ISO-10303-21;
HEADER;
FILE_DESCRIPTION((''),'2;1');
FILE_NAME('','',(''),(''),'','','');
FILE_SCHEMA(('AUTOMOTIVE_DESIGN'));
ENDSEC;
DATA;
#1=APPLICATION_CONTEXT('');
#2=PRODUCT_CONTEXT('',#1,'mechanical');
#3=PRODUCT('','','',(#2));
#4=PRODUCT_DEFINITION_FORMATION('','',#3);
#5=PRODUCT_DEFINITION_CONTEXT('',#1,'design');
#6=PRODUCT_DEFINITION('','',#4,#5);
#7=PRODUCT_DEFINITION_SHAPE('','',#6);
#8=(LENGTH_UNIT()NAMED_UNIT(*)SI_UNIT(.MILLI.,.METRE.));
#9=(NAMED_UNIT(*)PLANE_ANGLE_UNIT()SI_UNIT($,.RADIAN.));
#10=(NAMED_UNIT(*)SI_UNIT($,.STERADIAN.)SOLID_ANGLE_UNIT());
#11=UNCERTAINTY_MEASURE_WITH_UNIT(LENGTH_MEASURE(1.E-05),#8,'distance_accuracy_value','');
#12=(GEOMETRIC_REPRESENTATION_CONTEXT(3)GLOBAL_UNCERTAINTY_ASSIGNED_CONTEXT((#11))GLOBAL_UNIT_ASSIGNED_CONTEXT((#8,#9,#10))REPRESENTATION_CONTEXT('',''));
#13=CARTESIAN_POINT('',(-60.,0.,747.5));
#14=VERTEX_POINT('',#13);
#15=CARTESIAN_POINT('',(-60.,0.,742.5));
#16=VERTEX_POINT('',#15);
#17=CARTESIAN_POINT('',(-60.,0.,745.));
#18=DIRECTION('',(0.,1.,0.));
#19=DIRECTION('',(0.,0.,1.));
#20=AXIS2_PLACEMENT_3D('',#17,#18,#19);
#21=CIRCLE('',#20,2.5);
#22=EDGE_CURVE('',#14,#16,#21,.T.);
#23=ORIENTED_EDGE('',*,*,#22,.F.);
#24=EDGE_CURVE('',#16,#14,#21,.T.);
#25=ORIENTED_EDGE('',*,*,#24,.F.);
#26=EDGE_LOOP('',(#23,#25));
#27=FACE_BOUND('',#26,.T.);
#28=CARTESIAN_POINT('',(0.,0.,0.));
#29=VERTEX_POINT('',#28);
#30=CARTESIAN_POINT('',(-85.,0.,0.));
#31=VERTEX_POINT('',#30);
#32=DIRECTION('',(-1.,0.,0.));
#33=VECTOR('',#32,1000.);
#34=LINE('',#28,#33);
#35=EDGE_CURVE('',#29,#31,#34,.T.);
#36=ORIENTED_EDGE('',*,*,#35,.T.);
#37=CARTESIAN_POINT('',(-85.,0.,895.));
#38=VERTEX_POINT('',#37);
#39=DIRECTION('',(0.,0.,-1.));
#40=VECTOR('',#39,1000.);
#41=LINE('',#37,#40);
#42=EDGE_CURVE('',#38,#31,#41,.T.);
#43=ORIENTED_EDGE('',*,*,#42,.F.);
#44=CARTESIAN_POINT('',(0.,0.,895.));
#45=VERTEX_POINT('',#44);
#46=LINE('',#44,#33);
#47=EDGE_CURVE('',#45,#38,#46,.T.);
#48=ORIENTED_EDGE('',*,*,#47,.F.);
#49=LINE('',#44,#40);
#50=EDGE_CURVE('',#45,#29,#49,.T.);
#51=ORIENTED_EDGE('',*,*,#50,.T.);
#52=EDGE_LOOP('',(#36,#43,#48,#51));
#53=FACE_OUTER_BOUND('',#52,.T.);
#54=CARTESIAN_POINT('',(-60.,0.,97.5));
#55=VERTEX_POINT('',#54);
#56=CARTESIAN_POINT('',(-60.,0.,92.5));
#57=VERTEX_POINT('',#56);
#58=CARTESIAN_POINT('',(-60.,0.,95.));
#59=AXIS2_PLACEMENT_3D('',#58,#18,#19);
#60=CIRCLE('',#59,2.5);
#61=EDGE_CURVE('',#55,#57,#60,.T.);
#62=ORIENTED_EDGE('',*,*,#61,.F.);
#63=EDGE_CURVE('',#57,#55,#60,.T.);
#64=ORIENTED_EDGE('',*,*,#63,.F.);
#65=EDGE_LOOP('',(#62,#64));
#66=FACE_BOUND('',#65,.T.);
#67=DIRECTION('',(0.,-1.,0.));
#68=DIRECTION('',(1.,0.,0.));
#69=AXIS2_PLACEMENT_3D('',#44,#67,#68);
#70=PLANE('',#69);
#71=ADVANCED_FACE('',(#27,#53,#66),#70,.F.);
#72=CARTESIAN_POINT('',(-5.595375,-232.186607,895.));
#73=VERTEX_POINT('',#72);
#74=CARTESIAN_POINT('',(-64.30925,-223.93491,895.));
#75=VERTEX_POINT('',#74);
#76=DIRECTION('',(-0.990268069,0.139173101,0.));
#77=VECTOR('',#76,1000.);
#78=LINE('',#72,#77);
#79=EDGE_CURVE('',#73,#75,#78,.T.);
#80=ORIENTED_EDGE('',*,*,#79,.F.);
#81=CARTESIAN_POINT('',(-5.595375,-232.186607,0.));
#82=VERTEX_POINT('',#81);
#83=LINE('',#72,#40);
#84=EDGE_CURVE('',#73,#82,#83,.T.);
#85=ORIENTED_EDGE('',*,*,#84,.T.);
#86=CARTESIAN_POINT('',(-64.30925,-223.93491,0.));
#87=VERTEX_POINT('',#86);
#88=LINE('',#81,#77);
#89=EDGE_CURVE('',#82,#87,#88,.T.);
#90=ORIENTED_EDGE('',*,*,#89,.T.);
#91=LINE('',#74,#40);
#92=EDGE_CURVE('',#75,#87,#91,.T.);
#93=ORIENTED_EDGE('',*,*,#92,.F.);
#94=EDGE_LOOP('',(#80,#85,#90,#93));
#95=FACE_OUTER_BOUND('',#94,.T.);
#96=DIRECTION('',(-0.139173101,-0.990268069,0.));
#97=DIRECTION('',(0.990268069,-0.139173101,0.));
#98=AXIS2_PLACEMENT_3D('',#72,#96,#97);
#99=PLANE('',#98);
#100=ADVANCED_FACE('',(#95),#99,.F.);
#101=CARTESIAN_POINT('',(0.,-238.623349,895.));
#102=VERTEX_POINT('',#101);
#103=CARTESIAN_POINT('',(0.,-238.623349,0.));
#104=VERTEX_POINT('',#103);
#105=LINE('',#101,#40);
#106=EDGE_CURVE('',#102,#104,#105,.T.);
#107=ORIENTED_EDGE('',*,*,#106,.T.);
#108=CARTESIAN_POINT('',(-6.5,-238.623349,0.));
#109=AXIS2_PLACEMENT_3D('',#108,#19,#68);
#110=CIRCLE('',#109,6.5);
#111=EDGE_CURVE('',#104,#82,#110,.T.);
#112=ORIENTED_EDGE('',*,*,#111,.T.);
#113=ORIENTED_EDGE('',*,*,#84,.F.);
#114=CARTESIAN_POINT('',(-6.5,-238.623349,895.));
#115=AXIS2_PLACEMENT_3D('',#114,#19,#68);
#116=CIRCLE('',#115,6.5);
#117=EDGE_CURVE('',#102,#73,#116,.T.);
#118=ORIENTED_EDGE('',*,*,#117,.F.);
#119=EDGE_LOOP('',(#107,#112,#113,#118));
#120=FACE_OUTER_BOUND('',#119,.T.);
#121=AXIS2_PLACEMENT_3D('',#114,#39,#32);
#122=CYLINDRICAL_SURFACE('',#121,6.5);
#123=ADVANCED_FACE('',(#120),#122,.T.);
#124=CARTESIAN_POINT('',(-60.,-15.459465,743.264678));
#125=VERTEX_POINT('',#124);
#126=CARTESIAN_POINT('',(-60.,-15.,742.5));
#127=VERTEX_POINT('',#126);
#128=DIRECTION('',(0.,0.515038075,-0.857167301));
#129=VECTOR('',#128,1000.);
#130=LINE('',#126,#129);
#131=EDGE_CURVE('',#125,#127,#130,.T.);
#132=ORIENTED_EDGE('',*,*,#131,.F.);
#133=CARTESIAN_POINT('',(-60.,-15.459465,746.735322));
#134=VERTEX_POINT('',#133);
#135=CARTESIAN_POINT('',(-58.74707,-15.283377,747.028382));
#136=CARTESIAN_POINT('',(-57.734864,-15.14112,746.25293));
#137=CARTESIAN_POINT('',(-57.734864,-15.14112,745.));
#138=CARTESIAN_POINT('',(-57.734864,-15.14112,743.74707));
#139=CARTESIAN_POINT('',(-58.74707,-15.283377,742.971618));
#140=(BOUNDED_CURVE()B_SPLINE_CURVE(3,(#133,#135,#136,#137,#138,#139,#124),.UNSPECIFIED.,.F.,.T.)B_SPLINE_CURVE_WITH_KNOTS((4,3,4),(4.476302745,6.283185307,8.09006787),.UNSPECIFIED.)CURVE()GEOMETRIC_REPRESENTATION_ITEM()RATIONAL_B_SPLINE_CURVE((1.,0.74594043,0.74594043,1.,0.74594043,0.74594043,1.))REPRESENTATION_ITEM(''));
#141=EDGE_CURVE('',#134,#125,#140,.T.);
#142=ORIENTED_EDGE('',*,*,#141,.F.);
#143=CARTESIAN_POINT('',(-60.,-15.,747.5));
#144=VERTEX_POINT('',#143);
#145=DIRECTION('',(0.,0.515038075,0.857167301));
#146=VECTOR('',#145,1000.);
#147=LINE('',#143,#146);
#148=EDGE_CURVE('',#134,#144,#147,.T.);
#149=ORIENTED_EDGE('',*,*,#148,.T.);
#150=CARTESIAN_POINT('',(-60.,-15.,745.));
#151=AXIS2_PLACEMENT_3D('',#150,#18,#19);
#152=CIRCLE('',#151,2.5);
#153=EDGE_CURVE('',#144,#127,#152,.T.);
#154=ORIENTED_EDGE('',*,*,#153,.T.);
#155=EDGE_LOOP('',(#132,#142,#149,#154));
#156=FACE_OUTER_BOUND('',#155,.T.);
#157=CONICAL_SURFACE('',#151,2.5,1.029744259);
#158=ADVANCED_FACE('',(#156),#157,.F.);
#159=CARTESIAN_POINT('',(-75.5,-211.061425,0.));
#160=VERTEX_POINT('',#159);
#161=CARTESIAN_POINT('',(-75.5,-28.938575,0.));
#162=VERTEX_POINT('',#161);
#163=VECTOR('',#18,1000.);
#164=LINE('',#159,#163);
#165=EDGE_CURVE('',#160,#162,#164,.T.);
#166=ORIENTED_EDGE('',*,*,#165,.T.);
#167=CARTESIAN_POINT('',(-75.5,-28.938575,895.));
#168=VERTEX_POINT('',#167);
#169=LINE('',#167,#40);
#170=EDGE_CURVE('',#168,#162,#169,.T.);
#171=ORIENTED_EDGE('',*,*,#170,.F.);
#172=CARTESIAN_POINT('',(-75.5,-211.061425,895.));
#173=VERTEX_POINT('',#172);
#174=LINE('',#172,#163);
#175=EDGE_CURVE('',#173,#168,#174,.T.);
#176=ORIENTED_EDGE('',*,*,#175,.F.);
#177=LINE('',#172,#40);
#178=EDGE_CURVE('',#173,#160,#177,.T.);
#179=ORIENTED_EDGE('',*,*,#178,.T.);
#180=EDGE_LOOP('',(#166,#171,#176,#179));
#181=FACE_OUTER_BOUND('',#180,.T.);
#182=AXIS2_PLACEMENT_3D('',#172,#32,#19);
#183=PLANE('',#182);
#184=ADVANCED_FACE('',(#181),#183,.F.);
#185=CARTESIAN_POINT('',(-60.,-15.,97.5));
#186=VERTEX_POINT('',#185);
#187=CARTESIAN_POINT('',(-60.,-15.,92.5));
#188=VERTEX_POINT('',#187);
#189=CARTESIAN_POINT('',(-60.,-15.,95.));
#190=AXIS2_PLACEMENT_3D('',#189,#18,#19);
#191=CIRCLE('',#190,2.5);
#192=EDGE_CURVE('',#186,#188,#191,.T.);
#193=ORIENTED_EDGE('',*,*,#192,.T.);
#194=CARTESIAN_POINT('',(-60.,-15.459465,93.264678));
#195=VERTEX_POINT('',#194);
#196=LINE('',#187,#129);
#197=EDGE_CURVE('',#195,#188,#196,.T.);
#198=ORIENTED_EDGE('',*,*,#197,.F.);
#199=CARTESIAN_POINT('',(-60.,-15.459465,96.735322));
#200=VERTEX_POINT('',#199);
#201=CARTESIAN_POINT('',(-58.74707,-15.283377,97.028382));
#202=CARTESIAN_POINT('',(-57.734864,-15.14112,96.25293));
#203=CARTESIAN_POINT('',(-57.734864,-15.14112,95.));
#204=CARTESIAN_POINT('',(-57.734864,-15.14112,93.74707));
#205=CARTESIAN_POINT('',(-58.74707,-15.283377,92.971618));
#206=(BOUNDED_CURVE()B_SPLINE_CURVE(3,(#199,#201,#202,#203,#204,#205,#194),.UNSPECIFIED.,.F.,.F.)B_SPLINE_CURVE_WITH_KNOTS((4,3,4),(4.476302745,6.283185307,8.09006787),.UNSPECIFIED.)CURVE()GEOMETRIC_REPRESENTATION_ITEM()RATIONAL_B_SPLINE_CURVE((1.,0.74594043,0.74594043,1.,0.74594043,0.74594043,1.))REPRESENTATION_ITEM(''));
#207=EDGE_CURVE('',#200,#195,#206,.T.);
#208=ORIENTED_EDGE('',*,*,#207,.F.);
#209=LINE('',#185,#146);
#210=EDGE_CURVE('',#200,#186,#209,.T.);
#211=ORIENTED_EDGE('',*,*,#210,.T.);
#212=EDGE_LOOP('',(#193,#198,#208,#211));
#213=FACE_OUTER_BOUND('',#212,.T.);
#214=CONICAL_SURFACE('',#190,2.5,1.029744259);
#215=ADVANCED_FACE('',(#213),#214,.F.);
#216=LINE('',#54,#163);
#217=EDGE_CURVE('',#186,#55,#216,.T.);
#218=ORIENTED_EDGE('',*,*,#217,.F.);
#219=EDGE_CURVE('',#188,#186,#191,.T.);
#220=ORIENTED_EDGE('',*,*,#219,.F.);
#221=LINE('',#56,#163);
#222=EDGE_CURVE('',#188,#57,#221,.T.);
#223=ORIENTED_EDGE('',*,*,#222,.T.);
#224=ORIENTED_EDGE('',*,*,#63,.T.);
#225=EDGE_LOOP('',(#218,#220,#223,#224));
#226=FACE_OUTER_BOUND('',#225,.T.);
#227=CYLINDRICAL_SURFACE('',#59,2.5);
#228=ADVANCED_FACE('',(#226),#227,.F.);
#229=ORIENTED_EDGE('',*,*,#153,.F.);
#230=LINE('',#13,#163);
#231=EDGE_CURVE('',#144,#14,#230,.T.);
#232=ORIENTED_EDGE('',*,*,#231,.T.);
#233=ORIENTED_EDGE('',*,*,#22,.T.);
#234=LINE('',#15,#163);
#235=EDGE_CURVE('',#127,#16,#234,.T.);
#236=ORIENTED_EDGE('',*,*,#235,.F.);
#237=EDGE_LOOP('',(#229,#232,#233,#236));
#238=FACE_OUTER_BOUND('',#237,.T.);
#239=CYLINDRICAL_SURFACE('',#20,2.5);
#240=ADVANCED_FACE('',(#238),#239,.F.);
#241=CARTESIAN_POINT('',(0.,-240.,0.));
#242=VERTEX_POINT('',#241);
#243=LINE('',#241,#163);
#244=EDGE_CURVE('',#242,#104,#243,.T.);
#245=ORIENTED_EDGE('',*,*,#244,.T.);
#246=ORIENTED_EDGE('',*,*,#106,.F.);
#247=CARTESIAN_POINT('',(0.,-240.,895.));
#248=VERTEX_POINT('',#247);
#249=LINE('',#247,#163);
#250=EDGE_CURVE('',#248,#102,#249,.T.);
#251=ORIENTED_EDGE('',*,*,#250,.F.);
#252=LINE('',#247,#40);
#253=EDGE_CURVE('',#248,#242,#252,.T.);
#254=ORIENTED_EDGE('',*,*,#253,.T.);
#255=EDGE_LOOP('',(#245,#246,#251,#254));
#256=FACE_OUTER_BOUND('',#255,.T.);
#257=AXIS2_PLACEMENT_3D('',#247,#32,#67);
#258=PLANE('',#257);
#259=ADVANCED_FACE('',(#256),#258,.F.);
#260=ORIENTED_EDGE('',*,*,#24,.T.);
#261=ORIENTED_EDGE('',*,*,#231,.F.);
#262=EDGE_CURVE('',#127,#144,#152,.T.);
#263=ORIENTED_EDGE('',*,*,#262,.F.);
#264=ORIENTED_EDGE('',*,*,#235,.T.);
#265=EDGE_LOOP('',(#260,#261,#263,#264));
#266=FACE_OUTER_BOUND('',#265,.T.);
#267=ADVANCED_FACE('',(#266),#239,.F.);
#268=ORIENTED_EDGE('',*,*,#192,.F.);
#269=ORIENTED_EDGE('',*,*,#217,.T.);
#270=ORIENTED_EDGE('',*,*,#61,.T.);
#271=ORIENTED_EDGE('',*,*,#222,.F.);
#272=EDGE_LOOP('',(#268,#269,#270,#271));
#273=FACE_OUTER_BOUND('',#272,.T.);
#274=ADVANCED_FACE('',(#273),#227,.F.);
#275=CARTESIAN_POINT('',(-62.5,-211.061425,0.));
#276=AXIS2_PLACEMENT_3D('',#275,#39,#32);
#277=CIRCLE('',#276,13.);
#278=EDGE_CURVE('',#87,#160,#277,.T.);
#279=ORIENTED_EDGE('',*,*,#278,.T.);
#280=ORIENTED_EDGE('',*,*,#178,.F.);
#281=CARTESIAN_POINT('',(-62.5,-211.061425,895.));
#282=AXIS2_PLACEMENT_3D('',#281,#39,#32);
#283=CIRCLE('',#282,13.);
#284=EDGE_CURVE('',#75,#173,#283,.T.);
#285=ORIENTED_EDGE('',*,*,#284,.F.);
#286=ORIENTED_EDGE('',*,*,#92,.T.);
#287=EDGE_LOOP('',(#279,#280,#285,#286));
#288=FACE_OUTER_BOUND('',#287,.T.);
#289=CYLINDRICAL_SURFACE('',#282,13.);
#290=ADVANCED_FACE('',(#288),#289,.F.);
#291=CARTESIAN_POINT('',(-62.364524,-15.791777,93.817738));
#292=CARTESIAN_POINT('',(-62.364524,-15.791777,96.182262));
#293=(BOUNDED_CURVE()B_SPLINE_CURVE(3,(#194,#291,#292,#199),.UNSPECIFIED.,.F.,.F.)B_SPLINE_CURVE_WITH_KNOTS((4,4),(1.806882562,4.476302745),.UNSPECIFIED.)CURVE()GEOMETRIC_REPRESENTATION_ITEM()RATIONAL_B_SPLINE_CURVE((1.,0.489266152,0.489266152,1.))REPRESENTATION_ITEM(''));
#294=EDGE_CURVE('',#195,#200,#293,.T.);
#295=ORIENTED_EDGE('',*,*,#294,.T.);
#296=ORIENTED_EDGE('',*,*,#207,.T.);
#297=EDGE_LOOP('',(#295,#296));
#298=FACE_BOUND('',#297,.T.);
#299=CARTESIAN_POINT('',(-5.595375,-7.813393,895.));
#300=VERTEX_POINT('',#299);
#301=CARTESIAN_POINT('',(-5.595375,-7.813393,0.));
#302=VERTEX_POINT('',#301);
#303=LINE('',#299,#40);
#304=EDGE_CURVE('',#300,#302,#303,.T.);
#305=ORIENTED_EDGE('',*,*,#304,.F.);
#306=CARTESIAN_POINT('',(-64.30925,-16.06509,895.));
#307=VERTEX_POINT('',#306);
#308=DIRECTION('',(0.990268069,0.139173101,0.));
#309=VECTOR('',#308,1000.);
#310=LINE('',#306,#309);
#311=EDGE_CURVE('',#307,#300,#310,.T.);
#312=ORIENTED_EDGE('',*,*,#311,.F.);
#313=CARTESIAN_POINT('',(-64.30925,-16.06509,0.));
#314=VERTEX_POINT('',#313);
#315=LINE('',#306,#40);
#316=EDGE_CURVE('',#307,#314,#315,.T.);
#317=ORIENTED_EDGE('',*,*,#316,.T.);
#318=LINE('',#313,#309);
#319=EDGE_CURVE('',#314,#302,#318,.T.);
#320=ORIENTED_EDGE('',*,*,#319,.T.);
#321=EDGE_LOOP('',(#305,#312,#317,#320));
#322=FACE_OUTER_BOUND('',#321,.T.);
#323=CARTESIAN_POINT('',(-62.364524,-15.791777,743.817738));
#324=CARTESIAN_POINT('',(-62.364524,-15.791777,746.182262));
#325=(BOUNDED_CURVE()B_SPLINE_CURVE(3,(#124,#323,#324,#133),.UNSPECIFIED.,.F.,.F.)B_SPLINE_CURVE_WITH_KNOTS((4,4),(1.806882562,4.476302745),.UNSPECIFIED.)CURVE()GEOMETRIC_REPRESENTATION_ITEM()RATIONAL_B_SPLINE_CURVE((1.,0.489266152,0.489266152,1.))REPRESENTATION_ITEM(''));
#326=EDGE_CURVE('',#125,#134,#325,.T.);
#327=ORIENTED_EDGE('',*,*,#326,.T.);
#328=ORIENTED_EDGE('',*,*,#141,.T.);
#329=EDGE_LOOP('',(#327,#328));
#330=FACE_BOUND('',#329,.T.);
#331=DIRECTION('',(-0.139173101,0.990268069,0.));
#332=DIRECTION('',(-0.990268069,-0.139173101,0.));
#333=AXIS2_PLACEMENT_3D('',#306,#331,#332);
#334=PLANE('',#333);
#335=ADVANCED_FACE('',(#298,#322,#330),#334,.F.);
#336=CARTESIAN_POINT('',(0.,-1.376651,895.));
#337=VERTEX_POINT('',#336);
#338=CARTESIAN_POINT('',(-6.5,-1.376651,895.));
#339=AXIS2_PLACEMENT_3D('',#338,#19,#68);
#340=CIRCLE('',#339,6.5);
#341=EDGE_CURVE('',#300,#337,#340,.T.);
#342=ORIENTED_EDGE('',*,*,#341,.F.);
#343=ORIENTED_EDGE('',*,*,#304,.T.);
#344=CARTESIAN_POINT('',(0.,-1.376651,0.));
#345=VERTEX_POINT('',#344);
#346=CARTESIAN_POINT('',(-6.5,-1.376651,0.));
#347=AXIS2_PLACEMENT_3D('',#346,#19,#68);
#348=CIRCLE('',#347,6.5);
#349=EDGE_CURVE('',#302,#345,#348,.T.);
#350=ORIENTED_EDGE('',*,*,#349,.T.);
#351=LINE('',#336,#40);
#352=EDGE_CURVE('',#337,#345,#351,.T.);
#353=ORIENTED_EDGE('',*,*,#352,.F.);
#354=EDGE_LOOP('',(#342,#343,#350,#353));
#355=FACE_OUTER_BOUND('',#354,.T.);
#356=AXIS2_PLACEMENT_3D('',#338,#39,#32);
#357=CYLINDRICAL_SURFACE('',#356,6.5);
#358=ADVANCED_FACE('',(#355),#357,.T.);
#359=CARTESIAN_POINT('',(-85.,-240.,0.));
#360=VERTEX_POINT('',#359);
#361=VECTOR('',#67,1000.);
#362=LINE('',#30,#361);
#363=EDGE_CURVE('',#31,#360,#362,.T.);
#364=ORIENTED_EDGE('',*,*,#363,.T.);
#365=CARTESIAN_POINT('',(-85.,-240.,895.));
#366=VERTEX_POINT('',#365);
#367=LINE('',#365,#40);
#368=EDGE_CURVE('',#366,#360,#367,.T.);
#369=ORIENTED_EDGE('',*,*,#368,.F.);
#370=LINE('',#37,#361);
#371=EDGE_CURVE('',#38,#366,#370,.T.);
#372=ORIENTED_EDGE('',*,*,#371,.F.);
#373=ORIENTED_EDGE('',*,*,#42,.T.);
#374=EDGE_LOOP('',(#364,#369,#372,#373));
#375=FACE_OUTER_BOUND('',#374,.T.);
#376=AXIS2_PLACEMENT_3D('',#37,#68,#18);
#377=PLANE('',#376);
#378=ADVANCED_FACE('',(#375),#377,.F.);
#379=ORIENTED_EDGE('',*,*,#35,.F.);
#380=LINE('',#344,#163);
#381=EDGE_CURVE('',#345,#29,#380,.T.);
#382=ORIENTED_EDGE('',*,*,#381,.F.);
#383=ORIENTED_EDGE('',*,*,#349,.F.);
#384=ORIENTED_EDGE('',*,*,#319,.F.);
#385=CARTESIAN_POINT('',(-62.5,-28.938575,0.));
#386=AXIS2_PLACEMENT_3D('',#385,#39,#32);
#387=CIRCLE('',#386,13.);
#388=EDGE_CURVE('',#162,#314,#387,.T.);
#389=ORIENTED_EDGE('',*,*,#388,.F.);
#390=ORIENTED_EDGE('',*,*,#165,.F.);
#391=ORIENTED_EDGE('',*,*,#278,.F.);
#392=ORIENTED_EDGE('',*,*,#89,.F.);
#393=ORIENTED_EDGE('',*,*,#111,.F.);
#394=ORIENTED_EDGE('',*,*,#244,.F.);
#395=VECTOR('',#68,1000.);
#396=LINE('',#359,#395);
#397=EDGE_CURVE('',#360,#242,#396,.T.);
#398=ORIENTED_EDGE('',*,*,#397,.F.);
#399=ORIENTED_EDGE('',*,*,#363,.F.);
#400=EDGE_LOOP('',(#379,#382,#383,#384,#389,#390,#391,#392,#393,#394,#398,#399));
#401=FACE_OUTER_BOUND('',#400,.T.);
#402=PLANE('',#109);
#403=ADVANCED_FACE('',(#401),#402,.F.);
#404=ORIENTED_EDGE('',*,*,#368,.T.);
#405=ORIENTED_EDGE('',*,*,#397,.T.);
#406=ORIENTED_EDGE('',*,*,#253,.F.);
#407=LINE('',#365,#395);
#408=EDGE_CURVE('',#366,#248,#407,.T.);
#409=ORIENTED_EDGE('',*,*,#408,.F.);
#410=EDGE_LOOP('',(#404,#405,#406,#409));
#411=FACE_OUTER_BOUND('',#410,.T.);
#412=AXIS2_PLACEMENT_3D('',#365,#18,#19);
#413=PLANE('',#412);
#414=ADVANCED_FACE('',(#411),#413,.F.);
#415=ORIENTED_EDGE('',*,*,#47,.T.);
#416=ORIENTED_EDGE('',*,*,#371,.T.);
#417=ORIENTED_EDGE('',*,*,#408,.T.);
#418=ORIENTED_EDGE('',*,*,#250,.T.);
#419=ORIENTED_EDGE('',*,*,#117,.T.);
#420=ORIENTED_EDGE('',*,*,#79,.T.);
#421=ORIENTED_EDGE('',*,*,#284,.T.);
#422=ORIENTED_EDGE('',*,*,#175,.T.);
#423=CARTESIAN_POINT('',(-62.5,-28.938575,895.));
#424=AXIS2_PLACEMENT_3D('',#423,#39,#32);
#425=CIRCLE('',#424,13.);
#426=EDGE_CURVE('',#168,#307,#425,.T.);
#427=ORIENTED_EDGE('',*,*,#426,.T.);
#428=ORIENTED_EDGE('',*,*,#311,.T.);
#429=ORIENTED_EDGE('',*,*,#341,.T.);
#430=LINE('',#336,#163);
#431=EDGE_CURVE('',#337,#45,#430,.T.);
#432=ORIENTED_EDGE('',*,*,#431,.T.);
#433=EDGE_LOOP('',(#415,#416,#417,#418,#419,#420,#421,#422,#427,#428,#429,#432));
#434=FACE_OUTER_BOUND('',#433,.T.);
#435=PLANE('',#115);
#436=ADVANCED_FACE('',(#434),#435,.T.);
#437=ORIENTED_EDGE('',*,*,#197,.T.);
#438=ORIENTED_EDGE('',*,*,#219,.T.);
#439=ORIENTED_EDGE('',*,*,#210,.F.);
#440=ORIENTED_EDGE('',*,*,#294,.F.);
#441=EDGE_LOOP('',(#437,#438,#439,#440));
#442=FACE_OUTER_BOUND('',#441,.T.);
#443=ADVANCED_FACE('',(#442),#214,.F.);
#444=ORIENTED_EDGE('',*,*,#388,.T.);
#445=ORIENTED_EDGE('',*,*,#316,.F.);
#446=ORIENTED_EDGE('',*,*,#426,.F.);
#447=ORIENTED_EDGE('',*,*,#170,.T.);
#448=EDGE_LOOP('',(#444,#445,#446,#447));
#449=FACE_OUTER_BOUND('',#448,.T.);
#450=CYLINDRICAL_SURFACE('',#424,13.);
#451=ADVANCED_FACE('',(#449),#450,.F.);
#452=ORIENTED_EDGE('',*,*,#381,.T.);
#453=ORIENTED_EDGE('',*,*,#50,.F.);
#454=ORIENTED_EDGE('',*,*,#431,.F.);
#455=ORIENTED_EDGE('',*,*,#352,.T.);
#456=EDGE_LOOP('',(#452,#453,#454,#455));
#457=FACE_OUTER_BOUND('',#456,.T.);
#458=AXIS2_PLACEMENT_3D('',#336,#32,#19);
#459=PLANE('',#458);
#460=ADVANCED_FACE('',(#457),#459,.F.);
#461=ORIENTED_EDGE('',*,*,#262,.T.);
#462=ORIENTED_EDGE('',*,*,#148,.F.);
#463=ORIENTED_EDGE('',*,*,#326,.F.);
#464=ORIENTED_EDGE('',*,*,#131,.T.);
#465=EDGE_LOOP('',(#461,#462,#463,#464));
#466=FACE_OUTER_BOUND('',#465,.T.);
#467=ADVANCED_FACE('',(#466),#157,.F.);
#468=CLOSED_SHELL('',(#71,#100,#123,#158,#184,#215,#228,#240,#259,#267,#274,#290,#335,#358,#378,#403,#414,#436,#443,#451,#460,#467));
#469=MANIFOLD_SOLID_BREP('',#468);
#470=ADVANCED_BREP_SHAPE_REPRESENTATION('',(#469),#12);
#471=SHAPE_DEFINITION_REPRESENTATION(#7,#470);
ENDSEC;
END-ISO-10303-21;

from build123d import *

# Parameters (mm, degrees)
EXTRUDE_1_DEPTH        = 895
HOLE_WIZARD_M6_1_D     = 5
HOLE_WIZARD_M6_1_DEPTH = 15
HOLE_WIZARD_M6_1_TIP   = 1.502151548


with BuildPart() as part:
    # 草图1 → 凸台-拉伸1 (new body)
    with BuildSketch(Plane.XY):
        with BuildLine():
            Line((0, 0), (-85, 0))
            Line((-85, 0), (-85, -240))
            Line((-85, -240), (0, -240))
            Line((0, -240), (0, -238.623349271))
            ThreePointArc((0, -238.623349271), (-1.594387729, -234.358965582), (-5.595374844, -232.186606824))
            Line((-5.595374844, -232.186606824), (-64.309250312, -223.934909757))
            ThreePointArc((-64.309250312, -223.934909757), (-72.311224543, -219.59019224), (-75.5, -211.061424863))
            Line((-75.5, -211.061424863), (-75.5, -28.938575137))
            ThreePointArc((-75.5, -28.938575137), (-72.311224543, -20.40980776), (-64.309250312, -16.065090243))
            Line((-64.309250312, -16.065090243), (-5.595374844, -7.813393176))
            ThreePointArc((-5.595374844, -7.813393176), (-1.594387729, -5.641034418), (0, -1.376650729))
            Line((0, -1.376650729), (0, 0))
        make_face()
    extrude(amount=EXTRUDE_1_DEPTH)

    # M6 螺纹孔1
    with Locations(Plane(origin=(0, 0, 0), x_dir=(1, 0, 0), z_dir=(0, 1, 0))):
        with Locations((-60, -745), (-60, -95)):
            Hole(HOLE_WIZARD_M6_1_D / 2, depth=HOLE_WIZARD_M6_1_DEPTH)
            with Locations((0, 0, -(HOLE_WIZARD_M6_1_DEPTH + HOLE_WIZARD_M6_1_TIP / 2))):  # 118° drill point
                Cone(0, HOLE_WIZARD_M6_1_D / 2, HOLE_WIZARD_M6_1_TIP, mode=Mode.SUBTRACT)


solid = part.part
